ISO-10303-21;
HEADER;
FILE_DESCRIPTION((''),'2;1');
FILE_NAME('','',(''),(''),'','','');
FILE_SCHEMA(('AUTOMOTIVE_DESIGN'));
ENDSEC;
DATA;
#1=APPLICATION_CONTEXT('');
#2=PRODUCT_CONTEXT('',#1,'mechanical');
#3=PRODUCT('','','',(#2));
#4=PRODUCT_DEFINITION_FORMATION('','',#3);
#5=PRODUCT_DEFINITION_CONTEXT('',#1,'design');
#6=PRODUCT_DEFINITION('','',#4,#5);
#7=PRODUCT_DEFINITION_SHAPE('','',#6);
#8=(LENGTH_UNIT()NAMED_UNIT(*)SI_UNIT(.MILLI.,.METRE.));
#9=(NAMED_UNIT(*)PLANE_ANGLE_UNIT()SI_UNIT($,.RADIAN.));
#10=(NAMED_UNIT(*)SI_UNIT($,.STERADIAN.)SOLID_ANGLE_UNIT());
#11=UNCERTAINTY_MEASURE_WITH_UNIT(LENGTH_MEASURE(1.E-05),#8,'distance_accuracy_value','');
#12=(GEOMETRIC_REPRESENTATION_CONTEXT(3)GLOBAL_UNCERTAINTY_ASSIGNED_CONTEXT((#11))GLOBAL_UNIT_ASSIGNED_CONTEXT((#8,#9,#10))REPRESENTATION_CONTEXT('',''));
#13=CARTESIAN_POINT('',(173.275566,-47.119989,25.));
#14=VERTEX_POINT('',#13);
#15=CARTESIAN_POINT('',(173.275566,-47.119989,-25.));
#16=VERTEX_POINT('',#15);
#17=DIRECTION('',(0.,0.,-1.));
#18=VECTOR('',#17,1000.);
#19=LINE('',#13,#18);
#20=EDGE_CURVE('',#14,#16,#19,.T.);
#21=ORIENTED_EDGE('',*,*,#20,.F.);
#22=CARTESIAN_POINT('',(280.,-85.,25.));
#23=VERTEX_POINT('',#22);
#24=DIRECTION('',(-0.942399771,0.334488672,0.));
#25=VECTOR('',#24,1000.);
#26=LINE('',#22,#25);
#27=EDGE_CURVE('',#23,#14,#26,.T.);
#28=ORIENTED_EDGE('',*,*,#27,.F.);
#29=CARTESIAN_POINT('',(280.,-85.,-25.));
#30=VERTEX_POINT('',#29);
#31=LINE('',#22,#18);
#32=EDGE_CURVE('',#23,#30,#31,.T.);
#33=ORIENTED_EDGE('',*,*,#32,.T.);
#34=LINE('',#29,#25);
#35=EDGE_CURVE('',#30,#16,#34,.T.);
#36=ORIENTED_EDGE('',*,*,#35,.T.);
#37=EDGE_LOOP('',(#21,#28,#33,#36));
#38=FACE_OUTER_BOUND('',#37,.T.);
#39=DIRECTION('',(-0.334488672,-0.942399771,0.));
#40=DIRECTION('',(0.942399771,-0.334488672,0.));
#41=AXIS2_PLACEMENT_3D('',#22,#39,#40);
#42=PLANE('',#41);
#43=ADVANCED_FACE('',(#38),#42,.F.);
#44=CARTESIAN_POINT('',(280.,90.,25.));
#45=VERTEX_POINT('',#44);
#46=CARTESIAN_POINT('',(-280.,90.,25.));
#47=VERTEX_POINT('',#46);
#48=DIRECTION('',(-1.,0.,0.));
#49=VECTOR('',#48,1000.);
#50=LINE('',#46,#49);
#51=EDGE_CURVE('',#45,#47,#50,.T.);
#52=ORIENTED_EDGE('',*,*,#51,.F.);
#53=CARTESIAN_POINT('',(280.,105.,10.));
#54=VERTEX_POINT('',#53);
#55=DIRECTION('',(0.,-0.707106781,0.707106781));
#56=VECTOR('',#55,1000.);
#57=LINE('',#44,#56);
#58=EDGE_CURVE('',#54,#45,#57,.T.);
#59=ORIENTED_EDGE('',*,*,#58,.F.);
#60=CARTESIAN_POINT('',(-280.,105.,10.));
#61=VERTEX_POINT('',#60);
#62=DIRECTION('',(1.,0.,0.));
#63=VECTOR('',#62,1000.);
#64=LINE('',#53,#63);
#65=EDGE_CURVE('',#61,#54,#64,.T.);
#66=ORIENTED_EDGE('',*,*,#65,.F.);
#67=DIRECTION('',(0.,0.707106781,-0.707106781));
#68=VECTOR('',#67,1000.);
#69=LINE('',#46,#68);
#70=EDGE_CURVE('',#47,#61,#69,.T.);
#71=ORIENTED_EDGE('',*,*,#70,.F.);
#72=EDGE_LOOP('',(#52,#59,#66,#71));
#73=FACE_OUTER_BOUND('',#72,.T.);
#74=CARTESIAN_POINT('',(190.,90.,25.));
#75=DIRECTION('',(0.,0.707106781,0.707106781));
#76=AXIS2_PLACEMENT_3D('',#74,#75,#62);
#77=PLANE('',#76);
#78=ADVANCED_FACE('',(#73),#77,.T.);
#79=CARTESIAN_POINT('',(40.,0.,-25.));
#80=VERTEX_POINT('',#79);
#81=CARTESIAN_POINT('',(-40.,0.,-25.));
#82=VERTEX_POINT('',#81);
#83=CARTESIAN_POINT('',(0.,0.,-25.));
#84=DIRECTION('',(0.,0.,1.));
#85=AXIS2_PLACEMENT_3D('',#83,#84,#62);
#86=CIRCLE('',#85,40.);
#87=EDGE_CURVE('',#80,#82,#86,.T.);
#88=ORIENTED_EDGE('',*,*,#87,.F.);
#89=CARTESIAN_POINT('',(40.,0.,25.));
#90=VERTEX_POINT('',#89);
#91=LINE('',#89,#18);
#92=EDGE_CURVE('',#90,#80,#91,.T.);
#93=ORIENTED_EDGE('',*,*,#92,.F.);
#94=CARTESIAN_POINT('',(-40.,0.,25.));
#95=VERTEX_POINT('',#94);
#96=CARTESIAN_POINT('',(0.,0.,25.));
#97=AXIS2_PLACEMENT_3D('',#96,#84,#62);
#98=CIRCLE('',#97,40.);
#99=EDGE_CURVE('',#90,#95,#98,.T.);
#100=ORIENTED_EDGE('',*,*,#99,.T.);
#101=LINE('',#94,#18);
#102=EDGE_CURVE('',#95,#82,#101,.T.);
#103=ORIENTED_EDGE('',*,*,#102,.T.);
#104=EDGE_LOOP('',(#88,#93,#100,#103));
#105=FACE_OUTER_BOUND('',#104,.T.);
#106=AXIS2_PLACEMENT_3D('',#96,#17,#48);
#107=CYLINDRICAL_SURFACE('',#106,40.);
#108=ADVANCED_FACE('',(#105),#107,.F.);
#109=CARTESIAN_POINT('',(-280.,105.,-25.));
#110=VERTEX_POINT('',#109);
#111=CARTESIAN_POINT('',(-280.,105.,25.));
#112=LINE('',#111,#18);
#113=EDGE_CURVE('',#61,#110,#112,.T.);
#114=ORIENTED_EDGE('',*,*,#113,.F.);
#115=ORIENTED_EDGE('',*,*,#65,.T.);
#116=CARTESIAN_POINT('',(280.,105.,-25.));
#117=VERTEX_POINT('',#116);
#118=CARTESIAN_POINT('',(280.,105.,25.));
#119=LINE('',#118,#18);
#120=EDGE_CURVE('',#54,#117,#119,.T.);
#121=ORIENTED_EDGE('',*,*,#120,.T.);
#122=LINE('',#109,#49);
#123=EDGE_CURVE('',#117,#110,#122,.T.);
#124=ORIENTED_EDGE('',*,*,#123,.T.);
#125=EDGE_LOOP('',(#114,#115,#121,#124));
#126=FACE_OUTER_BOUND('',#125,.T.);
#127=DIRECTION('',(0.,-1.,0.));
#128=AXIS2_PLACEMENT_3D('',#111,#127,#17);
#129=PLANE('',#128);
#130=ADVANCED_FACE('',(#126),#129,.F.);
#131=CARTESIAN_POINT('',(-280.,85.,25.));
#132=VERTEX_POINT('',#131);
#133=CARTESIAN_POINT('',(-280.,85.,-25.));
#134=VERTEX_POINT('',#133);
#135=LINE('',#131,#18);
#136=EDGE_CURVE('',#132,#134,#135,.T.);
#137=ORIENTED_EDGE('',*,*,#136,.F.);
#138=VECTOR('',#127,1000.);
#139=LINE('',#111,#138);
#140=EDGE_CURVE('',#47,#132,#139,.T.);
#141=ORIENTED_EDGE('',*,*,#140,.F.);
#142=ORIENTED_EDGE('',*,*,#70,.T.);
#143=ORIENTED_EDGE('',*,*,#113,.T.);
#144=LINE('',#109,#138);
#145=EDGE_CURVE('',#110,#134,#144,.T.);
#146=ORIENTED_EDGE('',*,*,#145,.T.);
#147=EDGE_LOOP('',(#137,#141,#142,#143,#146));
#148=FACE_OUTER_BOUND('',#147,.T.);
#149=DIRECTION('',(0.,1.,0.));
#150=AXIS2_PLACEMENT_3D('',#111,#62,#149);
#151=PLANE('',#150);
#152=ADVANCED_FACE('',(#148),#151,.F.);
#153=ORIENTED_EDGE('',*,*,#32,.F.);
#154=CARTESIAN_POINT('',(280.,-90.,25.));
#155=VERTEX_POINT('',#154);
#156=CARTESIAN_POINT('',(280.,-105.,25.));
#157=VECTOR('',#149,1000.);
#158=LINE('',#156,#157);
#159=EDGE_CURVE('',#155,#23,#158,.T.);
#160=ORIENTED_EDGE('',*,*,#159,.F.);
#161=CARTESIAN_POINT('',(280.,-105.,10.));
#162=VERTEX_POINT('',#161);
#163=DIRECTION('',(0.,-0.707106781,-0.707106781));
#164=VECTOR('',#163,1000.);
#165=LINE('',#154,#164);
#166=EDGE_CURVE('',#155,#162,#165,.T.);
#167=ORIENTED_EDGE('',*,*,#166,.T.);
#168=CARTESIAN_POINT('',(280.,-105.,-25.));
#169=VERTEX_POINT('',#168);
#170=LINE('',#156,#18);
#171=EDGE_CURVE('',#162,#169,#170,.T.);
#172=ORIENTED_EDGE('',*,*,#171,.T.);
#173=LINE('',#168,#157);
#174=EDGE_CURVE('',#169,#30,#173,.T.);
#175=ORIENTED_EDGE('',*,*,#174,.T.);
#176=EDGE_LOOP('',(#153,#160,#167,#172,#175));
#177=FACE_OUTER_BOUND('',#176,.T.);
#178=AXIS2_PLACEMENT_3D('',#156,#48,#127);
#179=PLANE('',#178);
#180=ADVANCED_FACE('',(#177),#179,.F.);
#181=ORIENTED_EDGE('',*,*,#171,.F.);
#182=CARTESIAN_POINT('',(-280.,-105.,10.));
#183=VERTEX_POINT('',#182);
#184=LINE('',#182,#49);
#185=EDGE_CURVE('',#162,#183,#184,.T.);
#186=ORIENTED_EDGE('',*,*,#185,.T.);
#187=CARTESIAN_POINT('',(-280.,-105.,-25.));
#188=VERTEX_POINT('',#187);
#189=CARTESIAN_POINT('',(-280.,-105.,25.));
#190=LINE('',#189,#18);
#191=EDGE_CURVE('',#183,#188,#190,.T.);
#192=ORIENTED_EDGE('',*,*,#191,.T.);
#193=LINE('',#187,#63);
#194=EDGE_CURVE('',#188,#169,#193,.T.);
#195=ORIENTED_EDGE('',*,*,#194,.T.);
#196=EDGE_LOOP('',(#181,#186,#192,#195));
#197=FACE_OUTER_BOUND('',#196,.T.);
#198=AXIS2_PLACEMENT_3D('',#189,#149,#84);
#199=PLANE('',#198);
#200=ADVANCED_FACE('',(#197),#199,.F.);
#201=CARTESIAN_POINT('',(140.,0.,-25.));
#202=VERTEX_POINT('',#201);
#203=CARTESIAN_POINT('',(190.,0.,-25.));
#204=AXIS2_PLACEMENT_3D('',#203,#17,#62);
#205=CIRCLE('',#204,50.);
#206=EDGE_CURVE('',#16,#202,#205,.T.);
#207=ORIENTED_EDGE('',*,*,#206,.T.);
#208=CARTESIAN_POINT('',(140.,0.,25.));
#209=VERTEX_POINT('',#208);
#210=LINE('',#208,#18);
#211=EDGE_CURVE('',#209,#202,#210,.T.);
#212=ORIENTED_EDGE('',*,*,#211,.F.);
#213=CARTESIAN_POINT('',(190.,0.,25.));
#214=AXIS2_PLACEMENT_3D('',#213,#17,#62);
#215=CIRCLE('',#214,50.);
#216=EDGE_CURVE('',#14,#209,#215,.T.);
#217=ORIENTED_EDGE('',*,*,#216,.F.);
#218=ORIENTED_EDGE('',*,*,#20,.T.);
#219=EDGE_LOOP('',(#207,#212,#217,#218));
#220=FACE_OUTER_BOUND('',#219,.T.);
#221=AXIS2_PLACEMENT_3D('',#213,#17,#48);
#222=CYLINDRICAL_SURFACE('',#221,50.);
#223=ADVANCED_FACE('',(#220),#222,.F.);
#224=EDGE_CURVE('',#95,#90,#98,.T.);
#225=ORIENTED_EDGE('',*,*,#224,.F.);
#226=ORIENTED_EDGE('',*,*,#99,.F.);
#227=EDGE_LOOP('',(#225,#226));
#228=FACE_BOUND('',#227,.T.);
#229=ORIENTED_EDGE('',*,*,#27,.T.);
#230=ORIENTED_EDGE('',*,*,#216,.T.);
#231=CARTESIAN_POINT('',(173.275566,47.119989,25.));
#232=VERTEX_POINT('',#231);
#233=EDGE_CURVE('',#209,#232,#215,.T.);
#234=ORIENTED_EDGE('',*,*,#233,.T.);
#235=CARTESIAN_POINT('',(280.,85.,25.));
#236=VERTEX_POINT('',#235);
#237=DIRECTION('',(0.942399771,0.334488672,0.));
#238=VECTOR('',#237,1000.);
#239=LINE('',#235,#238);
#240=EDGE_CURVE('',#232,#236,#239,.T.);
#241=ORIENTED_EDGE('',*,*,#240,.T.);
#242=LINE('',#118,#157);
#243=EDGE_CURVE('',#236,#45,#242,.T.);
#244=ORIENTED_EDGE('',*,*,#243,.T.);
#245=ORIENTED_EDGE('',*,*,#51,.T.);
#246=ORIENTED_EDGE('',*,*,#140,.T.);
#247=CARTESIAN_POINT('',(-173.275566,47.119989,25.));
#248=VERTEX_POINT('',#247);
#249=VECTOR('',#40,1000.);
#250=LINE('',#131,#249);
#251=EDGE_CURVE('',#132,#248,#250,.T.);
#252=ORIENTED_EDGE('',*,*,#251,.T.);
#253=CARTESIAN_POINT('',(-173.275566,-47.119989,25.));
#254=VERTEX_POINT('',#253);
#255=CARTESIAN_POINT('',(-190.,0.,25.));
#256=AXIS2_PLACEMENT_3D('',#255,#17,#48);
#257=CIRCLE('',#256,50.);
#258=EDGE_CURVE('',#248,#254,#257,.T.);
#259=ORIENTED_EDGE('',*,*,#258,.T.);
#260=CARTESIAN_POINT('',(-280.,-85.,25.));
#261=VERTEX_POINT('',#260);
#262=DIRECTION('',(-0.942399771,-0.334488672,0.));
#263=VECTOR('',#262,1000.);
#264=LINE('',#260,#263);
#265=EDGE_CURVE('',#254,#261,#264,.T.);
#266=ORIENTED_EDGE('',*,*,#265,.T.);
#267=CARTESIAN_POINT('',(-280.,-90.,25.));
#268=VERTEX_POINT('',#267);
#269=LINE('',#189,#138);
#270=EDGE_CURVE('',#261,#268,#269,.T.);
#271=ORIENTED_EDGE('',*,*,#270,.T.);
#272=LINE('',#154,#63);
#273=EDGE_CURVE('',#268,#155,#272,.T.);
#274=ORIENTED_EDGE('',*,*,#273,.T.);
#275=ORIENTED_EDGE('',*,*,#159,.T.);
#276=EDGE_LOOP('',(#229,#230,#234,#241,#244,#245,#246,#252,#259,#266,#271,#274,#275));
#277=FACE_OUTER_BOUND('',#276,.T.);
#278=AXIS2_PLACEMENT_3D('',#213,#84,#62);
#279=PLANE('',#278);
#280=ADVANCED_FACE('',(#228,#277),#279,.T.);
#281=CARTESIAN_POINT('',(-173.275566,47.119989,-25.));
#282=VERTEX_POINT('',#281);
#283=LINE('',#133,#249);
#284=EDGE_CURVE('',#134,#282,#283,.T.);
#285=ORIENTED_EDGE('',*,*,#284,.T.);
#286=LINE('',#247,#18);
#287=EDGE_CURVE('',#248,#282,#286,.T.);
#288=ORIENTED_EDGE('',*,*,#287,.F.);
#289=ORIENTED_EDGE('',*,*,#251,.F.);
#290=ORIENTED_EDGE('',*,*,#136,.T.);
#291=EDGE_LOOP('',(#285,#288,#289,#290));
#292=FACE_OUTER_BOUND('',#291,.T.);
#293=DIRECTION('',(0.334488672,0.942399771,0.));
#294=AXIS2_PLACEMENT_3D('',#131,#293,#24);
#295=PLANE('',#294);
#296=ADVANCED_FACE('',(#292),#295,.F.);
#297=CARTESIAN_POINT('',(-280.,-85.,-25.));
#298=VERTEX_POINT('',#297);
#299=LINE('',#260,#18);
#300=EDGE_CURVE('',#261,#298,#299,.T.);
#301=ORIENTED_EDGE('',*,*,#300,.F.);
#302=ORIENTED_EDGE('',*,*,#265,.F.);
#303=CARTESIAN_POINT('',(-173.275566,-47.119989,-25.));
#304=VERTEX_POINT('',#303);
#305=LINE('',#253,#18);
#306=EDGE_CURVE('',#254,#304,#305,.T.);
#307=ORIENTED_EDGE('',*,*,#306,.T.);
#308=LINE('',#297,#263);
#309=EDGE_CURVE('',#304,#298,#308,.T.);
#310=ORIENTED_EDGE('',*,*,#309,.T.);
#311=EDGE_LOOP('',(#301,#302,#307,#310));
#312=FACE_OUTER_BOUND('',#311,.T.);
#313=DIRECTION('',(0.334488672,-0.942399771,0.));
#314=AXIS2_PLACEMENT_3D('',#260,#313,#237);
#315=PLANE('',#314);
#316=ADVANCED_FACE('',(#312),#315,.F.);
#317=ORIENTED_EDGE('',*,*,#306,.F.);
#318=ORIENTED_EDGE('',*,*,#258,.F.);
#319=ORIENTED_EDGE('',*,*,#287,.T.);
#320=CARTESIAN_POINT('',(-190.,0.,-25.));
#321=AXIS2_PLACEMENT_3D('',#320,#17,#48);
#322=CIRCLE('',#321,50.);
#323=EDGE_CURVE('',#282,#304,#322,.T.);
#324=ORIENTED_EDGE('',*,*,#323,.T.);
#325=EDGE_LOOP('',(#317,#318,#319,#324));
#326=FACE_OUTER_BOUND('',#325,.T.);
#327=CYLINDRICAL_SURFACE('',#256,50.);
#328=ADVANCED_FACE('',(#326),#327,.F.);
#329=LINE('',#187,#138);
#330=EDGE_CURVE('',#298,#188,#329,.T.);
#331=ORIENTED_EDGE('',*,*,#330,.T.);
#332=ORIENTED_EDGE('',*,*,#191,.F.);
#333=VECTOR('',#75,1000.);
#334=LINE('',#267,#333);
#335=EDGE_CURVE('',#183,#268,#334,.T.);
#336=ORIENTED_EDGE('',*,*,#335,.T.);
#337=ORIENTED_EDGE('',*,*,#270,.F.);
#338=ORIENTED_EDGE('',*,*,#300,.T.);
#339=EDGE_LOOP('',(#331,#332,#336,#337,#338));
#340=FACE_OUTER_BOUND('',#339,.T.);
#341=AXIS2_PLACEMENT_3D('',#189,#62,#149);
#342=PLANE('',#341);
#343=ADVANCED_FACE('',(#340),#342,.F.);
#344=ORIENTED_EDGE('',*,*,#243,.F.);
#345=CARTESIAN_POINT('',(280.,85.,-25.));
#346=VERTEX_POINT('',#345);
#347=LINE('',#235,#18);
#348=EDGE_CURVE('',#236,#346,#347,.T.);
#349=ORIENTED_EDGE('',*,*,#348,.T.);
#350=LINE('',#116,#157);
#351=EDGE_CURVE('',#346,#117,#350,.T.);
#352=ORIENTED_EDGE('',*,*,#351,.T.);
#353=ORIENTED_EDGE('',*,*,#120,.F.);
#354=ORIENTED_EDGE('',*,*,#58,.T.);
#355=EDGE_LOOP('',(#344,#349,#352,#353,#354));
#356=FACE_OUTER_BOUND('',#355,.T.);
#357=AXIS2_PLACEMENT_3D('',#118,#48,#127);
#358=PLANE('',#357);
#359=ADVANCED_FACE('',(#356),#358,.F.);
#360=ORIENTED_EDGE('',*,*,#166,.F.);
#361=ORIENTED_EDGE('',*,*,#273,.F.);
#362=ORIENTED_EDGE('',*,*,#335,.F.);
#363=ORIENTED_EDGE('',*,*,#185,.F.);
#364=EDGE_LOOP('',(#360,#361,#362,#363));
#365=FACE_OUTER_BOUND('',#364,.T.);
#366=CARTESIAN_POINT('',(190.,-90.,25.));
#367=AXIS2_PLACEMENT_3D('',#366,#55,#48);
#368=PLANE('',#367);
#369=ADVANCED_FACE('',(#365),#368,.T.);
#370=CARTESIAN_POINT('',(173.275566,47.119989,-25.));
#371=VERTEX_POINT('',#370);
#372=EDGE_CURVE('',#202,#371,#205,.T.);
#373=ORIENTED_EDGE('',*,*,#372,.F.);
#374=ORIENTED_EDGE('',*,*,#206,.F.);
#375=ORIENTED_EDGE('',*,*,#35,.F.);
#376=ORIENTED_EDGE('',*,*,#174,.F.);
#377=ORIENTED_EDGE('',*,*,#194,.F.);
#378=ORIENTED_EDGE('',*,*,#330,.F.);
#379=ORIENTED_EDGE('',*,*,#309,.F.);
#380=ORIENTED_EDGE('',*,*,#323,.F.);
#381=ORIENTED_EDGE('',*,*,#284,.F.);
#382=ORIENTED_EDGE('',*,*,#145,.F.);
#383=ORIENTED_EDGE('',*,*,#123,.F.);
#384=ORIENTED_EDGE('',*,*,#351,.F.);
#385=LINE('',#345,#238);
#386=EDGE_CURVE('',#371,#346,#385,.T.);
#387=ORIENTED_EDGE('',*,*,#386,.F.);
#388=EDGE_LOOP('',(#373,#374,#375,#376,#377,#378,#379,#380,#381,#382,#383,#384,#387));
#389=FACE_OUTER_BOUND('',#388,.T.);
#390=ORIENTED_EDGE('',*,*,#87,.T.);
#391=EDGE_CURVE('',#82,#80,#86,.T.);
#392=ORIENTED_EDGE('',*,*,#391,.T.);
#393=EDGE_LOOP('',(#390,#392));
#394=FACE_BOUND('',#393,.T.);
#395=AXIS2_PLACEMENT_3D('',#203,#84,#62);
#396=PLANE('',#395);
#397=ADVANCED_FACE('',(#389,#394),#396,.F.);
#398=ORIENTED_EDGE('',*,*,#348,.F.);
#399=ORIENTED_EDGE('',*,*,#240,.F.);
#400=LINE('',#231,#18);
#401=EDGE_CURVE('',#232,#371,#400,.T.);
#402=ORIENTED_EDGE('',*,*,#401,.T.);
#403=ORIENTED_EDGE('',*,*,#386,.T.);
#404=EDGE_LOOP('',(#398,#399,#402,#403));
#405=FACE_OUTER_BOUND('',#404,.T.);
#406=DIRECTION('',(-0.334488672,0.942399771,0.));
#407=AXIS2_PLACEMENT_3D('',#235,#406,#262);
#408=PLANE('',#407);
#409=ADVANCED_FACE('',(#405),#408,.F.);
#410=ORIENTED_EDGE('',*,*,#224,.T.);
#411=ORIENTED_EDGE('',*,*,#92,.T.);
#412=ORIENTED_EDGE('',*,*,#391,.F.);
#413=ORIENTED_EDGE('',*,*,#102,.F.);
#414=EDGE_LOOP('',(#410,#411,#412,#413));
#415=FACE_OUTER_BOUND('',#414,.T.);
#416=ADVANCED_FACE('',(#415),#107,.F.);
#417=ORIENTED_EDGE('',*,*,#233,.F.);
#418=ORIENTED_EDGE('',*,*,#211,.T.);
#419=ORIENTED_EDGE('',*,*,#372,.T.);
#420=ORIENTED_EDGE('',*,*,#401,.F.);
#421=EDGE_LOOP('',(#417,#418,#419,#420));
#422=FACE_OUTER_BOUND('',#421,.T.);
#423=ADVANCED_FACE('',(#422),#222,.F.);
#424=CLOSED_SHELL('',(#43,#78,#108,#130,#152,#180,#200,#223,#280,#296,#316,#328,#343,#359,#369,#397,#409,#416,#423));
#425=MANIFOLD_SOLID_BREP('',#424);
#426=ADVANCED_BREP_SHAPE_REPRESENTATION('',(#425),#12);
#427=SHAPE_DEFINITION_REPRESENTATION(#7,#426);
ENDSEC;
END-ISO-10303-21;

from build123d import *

# Parameters (mm, degrees)
SKETCH1_R           = 40
BOSS_EXTRUDE1_DEPTH = 25
CHAMFER1_SIZE       = 15


with BuildPart() as part:
    # Sketch1 → Boss-Extrude1 (new, symmetric)
    with BuildSketch(Plane.XY):
        with BuildLine():
            Line((-280, 105), (280, 105))
            Line((280, 105), (280, 85))
            Line((280, 85), (173.275566379, 47.11998854))
            ThreePointArc((173.275566379, 47.11998854), (140, 0), (173.275566379, -47.11998854))
            Line((173.275566379, -47.11998854), (280, -85))
            Line((280, -85), (280, -105))
            Line((280, -105), (-280, -105))
            Line((-280, -105), (-280, -85))
            Line((-280, -85), (-173.275566379, -47.11998854))
            ThreePointArc((-173.275566379, -47.11998854), (-140, 0), (-173.275566379, 47.11998854))
            Line((-173.275566379, 47.11998854), (-280, 85))
            Line((-280, 85), (-280, 105))
        make_face()
        Circle(SKETCH1_R, mode=Mode.SUBTRACT)
    extrude(amount=BOSS_EXTRUDE1_DEPTH, both=True)

    # Chamfer1
    chamfer1_edges = [part.edges().sort_by_distance(p)[0] for p in [
        (0, 105, 25),
        (0, -105, 25),
    ]]
    chamfer(chamfer1_edges, length=CHAMFER1_SIZE)


solid = part.part
